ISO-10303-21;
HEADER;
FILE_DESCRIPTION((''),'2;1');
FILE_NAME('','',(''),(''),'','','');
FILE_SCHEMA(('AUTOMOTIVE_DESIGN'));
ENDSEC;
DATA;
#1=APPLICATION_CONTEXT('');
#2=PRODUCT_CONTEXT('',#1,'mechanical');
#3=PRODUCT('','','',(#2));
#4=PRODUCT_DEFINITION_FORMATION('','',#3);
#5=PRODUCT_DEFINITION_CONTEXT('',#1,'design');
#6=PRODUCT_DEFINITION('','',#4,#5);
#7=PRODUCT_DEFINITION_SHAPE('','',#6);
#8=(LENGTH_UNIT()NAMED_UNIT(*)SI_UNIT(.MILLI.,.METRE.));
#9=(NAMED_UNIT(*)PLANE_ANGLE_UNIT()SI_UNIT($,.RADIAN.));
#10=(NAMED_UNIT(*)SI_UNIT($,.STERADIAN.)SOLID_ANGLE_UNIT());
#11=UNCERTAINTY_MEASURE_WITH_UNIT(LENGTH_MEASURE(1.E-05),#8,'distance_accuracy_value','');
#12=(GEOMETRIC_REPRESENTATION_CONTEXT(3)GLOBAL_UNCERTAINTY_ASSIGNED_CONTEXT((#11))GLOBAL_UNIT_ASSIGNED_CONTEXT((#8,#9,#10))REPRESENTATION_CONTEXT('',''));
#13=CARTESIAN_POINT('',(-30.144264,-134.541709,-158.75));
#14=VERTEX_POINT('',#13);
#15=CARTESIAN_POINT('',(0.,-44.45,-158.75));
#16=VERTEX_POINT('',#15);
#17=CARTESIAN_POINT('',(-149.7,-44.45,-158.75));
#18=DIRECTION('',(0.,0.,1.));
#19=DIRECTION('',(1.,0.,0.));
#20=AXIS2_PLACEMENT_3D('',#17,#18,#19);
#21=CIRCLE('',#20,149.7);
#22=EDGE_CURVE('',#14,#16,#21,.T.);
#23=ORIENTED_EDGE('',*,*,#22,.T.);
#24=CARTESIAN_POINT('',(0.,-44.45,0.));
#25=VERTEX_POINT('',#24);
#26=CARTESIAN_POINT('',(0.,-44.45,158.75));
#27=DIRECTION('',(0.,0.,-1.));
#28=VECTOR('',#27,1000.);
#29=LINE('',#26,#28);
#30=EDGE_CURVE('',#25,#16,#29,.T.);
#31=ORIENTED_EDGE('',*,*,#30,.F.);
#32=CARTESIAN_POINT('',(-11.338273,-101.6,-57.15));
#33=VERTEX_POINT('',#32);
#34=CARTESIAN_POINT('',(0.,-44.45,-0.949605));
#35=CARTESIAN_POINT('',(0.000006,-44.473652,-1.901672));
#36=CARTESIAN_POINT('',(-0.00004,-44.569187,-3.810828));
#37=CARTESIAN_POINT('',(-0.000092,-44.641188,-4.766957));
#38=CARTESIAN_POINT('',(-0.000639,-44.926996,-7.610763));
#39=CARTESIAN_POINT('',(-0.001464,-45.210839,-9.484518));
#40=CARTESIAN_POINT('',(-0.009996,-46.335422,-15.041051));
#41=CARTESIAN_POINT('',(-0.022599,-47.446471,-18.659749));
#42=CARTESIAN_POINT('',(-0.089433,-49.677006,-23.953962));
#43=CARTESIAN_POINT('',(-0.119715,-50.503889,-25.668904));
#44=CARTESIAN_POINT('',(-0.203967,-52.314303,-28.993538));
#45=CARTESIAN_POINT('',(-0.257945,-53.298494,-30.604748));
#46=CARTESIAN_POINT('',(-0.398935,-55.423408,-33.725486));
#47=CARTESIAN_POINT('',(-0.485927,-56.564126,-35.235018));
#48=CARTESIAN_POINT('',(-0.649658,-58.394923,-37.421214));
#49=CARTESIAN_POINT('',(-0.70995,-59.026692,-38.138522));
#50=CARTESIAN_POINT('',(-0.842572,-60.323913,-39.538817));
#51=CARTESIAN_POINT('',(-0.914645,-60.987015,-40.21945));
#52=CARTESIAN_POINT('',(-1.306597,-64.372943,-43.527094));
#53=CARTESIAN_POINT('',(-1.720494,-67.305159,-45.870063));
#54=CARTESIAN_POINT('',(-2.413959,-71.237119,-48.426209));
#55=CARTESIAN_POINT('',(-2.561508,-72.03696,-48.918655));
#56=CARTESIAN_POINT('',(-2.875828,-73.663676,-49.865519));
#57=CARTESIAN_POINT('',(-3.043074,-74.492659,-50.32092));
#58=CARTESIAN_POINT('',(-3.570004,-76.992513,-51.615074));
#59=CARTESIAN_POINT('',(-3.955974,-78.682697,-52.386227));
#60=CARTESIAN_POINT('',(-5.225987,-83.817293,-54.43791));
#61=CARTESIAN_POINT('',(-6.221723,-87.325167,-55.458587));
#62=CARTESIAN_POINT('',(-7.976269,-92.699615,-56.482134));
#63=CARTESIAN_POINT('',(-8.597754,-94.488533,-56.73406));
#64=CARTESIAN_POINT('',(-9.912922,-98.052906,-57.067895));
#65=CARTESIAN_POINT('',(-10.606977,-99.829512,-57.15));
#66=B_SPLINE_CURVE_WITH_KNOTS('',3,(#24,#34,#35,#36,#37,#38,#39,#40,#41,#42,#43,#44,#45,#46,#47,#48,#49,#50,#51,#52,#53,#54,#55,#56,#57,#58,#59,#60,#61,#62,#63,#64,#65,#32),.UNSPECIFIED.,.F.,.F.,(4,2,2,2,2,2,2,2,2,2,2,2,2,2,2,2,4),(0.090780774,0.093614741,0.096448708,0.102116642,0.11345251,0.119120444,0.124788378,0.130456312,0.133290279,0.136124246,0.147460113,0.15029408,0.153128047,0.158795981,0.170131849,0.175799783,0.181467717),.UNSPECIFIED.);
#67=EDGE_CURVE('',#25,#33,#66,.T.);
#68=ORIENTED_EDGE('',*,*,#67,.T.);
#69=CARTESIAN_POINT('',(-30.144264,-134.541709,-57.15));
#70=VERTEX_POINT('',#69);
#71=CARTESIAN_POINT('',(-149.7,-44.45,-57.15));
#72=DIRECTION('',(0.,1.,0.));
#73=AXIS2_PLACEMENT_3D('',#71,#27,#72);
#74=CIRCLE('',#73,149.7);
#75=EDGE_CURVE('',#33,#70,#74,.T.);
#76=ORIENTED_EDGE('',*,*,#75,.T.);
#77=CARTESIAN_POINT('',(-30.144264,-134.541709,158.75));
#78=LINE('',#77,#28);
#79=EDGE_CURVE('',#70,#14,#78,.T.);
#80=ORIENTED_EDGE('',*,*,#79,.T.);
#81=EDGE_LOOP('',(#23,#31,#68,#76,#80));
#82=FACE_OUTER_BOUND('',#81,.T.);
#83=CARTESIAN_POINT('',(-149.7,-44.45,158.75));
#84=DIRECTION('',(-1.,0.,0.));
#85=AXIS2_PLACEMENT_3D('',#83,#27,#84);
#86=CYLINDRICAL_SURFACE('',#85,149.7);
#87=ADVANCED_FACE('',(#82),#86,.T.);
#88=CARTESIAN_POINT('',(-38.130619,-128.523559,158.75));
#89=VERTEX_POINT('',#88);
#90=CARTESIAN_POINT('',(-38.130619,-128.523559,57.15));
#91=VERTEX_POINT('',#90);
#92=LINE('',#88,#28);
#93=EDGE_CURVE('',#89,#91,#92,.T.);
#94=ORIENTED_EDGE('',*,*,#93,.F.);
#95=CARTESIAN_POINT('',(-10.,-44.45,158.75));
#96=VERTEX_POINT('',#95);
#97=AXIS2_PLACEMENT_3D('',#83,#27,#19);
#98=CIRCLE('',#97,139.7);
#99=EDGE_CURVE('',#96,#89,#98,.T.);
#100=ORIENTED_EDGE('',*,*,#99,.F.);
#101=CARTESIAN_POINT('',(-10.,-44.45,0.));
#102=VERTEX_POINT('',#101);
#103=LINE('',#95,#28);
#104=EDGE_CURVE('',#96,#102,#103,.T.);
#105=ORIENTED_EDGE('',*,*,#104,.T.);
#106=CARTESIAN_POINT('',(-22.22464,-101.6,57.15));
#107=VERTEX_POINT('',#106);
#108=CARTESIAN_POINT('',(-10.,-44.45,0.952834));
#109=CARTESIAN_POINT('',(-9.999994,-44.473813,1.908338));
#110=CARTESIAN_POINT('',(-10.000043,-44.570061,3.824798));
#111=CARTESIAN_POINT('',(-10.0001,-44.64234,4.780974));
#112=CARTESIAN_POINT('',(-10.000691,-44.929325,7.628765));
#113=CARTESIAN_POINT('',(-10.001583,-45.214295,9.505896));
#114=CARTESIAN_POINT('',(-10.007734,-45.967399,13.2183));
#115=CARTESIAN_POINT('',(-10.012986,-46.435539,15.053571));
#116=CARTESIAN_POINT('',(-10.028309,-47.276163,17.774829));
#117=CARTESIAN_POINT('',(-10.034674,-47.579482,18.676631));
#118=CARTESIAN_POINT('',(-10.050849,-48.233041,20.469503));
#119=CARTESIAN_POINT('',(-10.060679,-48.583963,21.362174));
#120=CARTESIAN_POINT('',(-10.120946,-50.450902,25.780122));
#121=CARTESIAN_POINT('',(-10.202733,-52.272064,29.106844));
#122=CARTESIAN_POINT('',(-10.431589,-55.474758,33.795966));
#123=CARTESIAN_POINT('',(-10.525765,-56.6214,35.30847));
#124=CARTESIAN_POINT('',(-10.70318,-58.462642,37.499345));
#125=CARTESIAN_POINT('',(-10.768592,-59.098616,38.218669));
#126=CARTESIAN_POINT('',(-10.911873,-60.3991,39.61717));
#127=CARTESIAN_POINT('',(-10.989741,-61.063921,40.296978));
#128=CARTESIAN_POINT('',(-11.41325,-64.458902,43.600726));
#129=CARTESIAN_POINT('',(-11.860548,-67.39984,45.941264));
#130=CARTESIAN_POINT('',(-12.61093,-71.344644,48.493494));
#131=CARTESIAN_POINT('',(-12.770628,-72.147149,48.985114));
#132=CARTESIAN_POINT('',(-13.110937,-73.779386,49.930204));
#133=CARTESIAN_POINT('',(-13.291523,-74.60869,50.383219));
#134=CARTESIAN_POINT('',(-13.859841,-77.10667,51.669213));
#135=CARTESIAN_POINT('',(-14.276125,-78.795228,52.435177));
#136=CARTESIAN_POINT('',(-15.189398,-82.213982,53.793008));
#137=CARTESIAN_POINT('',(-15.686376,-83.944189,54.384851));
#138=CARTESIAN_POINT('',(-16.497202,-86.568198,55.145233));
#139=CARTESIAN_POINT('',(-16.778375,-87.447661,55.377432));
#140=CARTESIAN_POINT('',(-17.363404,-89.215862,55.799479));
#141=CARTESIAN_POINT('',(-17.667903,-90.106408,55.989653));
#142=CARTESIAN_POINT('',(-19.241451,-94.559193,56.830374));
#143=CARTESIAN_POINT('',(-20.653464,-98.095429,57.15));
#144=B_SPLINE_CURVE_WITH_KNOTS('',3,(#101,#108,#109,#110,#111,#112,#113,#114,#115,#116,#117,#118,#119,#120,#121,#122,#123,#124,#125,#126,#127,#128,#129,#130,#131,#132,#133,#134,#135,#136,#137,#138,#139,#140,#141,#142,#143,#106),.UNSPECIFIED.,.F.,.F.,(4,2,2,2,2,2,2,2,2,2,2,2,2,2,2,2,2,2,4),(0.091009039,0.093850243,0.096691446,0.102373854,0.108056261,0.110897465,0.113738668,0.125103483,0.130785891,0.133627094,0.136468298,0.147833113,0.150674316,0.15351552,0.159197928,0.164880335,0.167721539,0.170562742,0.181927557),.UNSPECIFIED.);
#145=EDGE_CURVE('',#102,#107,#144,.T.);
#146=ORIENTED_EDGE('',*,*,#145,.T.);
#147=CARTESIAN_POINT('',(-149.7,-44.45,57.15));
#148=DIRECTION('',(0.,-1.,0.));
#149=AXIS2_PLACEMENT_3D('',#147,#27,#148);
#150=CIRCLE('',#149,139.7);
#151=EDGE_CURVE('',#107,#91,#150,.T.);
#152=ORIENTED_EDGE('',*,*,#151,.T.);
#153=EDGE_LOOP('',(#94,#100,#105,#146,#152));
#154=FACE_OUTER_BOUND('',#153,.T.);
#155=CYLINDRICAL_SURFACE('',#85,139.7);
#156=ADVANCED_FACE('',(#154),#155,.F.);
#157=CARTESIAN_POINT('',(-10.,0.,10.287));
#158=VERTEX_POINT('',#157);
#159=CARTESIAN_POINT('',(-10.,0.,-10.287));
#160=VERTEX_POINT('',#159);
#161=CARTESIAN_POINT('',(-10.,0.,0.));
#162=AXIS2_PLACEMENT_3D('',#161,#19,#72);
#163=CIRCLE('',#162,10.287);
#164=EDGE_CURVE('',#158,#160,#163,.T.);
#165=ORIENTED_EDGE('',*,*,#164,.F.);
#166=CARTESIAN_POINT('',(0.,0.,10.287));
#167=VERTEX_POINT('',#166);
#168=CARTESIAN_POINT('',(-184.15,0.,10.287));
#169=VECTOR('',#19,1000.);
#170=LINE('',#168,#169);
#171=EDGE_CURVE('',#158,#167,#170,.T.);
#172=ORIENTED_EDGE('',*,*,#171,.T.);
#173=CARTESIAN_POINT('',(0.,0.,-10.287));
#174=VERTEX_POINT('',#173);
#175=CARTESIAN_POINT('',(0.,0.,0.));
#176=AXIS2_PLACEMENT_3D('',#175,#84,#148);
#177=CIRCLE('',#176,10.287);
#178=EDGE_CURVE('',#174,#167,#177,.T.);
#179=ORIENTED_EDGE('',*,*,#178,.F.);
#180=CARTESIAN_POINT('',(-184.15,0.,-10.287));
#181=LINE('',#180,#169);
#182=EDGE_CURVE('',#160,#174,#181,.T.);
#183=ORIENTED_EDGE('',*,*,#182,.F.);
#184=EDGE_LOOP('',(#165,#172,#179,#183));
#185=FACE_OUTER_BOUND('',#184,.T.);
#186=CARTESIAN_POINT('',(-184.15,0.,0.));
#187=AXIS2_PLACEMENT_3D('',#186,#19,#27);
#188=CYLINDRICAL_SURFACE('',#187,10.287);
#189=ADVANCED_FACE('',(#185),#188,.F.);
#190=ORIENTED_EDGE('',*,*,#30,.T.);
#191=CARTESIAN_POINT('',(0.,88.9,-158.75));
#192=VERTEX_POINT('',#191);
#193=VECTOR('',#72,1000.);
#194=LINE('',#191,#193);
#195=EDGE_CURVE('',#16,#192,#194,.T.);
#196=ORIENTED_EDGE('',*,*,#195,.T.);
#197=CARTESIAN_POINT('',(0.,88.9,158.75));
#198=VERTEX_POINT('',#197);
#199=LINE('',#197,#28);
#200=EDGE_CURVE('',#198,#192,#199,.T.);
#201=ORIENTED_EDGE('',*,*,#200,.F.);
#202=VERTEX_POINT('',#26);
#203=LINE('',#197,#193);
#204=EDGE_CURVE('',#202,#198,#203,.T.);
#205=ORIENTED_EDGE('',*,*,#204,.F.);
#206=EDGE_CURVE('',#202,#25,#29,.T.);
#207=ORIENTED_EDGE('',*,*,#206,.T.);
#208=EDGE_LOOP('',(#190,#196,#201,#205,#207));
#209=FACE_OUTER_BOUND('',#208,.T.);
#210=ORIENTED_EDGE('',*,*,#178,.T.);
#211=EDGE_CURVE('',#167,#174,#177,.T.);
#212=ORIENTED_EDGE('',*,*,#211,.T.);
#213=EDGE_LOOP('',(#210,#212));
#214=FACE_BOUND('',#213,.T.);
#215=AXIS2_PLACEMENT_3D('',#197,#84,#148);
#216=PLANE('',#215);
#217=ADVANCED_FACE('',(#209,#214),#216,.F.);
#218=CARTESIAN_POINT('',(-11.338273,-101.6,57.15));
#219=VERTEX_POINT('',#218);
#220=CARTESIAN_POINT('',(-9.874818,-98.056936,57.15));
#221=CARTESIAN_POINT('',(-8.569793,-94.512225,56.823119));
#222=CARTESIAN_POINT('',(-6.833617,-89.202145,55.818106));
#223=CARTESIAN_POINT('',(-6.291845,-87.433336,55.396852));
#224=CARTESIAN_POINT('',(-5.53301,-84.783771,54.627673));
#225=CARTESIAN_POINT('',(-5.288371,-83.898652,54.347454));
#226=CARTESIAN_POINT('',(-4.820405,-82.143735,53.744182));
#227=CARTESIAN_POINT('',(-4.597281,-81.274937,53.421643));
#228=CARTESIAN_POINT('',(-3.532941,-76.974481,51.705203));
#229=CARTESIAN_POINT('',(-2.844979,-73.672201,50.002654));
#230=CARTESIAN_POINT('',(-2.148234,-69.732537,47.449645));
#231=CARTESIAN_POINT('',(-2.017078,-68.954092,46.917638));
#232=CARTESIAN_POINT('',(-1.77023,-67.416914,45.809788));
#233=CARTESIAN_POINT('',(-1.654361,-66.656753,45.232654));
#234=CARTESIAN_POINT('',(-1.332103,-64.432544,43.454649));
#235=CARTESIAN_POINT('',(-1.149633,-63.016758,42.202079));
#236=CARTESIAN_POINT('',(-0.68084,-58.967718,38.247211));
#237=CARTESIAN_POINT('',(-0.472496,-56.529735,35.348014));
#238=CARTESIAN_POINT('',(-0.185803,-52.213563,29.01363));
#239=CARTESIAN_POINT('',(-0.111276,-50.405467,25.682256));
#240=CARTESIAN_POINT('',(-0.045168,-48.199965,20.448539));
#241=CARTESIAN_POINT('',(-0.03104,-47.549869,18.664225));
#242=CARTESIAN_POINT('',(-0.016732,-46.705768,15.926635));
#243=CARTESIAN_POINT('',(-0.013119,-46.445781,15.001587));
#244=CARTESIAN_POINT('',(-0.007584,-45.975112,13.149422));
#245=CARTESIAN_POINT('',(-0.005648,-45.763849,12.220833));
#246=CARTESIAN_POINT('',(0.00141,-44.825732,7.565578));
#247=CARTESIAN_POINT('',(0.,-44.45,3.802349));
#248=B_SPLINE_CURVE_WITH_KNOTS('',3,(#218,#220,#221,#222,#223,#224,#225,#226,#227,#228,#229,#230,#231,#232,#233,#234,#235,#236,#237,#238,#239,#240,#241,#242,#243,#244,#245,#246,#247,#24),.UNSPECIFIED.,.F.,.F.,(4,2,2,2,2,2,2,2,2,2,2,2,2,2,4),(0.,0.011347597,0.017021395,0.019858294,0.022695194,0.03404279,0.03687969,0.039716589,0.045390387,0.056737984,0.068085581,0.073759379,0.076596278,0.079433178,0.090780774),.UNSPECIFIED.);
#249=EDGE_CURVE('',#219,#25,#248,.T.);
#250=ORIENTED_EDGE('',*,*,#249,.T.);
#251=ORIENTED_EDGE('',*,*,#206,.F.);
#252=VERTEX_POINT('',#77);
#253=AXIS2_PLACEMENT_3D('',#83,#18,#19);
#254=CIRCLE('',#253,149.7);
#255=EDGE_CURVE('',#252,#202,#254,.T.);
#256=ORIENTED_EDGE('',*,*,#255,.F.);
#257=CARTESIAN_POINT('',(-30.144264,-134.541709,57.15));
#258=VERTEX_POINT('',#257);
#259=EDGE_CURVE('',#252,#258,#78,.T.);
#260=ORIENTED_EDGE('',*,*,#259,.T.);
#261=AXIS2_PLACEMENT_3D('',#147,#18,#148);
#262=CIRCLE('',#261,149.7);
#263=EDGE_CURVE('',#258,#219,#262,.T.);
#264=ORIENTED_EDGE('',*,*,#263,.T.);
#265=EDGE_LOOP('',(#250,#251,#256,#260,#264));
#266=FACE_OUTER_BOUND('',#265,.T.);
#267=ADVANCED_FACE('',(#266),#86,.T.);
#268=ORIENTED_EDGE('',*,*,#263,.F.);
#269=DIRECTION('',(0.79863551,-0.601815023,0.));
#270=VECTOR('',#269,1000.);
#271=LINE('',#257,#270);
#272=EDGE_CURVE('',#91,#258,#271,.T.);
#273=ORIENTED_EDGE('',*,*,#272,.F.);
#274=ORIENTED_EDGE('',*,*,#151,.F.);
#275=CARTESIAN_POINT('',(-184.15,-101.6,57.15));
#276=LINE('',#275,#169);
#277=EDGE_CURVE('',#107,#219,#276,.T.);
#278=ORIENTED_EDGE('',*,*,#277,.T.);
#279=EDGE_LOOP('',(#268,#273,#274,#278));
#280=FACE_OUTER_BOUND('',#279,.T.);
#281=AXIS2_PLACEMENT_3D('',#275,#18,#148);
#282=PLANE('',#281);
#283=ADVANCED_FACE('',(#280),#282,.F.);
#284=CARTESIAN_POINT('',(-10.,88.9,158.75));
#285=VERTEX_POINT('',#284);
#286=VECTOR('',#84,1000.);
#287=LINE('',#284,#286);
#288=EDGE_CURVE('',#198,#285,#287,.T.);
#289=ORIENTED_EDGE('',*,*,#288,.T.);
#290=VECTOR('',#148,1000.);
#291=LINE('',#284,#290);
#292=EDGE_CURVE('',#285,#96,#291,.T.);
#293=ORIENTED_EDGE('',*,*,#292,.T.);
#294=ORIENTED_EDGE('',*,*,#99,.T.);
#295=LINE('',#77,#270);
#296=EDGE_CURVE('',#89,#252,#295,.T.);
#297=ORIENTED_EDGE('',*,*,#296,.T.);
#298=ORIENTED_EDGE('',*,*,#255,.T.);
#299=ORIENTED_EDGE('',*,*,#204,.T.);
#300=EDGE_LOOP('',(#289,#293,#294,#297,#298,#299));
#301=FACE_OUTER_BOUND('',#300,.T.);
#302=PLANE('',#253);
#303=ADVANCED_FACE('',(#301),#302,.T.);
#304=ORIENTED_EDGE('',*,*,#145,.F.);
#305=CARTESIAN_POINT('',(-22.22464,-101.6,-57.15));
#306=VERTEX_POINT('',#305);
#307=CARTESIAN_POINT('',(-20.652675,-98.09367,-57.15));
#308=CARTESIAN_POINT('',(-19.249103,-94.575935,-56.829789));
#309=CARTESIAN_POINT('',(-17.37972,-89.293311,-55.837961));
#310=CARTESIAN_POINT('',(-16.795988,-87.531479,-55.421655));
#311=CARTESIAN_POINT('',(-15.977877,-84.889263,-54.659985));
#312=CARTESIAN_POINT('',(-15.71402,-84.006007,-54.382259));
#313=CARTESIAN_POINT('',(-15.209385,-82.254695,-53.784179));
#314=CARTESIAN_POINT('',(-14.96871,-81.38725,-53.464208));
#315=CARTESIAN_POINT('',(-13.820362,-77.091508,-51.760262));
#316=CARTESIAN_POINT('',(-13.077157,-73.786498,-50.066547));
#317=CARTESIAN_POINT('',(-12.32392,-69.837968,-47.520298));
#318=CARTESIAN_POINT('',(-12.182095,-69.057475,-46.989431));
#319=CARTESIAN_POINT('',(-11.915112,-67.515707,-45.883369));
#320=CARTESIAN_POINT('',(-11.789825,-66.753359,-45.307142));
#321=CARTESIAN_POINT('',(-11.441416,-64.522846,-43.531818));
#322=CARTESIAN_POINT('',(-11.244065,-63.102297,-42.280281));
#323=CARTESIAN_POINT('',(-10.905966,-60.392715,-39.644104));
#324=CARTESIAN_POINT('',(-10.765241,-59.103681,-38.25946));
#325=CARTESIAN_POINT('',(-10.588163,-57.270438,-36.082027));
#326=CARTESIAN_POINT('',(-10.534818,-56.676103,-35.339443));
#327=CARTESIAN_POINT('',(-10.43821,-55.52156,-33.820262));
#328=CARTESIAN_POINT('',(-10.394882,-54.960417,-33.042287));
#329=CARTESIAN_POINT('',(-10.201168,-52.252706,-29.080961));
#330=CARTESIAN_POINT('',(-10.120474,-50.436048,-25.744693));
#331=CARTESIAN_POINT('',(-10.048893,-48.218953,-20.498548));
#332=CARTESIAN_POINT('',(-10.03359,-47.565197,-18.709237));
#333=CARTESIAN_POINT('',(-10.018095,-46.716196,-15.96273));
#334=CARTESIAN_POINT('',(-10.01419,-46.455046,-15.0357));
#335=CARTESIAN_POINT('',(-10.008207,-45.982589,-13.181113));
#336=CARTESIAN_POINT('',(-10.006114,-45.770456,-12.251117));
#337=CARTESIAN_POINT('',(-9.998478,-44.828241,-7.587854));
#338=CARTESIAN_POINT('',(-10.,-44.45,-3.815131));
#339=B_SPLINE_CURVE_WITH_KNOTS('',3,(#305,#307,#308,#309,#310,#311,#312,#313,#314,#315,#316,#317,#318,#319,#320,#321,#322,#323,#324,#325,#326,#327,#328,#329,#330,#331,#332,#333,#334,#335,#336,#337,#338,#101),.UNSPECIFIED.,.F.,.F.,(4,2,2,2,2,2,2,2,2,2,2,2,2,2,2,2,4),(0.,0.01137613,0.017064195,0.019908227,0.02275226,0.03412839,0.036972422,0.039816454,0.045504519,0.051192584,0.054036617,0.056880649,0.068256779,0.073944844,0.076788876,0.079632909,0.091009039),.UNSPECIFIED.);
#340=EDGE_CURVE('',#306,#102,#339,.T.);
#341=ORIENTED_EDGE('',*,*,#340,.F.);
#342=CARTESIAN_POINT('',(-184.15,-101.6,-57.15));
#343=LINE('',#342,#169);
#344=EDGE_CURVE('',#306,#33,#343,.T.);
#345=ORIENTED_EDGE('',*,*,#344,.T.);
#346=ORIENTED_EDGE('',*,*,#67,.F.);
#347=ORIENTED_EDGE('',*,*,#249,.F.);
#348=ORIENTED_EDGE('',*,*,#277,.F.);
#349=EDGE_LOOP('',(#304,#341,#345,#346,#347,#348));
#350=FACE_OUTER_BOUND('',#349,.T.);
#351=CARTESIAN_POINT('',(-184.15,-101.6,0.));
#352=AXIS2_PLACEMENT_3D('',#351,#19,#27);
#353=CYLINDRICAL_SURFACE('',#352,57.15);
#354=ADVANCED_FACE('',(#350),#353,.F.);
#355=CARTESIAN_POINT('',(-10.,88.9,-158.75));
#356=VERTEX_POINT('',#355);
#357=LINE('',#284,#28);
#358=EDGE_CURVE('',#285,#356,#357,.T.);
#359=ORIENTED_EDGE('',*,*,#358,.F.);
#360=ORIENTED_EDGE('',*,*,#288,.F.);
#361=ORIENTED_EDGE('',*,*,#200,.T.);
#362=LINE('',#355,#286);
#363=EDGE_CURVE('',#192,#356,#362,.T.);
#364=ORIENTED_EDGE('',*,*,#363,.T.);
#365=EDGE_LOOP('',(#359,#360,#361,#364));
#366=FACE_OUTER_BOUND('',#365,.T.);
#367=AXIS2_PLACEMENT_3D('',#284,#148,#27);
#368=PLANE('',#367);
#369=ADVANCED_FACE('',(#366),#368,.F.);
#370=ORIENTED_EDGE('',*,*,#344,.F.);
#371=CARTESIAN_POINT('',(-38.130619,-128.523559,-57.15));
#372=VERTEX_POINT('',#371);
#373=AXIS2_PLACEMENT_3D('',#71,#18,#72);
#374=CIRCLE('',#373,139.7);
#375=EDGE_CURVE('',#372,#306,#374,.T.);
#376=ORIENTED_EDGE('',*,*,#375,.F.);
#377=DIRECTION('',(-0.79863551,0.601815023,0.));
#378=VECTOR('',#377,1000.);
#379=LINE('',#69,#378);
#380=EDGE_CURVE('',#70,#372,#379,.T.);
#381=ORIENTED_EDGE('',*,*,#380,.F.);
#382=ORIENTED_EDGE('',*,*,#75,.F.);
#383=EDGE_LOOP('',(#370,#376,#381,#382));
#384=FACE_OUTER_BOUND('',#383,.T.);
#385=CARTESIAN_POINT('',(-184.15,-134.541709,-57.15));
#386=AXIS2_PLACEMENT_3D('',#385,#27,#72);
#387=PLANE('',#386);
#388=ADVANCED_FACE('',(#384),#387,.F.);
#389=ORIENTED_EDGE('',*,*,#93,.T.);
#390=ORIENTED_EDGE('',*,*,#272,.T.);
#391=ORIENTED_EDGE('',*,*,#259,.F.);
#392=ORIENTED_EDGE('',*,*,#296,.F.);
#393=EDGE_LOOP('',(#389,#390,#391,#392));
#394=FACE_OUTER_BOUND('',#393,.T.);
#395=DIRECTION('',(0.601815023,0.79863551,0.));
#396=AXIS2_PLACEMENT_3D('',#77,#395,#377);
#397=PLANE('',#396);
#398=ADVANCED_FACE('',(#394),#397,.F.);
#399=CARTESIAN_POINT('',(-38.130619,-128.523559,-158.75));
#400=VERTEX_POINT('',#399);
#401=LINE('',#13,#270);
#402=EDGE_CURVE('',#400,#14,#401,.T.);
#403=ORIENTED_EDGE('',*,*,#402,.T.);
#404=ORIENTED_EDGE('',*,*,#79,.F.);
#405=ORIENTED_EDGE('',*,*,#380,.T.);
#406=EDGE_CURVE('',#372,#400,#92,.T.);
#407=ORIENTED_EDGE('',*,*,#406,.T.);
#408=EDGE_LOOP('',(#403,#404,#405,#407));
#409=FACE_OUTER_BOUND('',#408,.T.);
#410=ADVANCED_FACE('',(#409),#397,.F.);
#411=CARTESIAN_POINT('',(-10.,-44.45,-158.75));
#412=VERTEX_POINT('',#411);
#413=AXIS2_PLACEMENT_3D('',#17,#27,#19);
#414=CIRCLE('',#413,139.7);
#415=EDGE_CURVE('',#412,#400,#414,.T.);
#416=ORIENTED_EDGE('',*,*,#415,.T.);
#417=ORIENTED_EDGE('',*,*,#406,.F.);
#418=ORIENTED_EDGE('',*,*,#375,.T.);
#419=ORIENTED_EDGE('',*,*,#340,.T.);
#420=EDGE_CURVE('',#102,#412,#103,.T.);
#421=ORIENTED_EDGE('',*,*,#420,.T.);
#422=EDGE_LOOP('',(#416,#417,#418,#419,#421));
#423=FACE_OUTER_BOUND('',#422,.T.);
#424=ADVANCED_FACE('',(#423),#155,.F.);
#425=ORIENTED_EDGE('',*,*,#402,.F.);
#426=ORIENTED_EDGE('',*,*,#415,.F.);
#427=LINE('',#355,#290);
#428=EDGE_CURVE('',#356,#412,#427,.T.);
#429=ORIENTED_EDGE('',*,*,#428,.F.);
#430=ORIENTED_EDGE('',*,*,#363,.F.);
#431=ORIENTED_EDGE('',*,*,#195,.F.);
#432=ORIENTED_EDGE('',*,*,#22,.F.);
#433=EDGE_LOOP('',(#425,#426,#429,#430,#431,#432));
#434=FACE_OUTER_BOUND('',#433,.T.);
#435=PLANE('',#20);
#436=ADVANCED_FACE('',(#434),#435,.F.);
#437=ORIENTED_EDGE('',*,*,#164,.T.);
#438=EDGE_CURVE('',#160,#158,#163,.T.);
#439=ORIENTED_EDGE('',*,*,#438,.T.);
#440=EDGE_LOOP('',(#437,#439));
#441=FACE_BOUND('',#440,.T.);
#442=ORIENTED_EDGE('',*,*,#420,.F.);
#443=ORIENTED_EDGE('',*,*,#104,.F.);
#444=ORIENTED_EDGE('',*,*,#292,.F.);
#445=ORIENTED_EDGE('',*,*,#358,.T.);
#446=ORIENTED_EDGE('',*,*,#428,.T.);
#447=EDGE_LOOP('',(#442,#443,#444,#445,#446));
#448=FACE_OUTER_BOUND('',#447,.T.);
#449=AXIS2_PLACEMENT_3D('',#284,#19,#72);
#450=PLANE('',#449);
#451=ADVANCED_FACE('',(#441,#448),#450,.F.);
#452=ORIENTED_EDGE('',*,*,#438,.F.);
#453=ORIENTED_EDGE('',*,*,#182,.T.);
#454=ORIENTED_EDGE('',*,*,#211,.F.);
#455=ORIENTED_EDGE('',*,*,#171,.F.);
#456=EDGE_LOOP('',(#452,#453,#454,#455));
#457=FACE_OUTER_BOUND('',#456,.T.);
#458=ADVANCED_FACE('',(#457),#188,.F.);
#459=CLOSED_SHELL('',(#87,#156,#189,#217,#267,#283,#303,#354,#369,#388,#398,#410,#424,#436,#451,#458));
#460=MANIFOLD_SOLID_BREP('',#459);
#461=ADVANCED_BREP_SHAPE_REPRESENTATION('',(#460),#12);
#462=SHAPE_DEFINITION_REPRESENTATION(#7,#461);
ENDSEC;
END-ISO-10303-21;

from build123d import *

# Parameters (mm, degrees)
BOSS_EXTRUDE1_DEPTH = 158.75
SKETCH4_R           = 10.287
CUT_EXTRUDE1_DEPTH  = 184.15


with BuildPart() as part:
    # Sketch1 → Boss-Extrude1 (new, symmetric)
    with BuildSketch(Plane.XY):
        with BuildLine():
            Line((-10, 88.9), (0, 88.9))
            Line((0, 88.9), (0, -44.45))
            ThreePointArc((0, -44.45), (-7.735948816, -91.950507064), (-30.144264146, -134.541708966))
            Line((-30.144264146, -134.541708966), (-38.130619246, -128.523558734))
            ThreePointArc((-38.130619246, -128.523558734), (-17.219185368, -88.7774605), (-10, -44.45))
            Line((-10, -44.45), (-10, 88.9))
        make_face()
    extrude(amount=BOSS_EXTRUDE1_DEPTH, both=True)

    # Sketch4 → Cut-Extrude1 (cut, symmetric)
    with BuildSketch(Plane(origin=(0, 0, 0), x_dir=(0, 0, -1), z_dir=(1, 0, 0))):
        Circle(SKETCH4_R)
        with BuildLine():
            Line((-57.15, -101.6), (-57.15, -134.541708966))
            Line((-57.15, -134.541708966), (57.15, -134.541708966))
            Line((57.15, -134.541708966), (57.15, -101.6))
            ThreePointArc((57.15, -101.6), (0, -44.45), (-57.15, -101.6))
        make_face()
    extrude(amount=CUT_EXTRUDE1_DEPTH, both=True, mode=Mode.SUBTRACT)


solid = part.part
